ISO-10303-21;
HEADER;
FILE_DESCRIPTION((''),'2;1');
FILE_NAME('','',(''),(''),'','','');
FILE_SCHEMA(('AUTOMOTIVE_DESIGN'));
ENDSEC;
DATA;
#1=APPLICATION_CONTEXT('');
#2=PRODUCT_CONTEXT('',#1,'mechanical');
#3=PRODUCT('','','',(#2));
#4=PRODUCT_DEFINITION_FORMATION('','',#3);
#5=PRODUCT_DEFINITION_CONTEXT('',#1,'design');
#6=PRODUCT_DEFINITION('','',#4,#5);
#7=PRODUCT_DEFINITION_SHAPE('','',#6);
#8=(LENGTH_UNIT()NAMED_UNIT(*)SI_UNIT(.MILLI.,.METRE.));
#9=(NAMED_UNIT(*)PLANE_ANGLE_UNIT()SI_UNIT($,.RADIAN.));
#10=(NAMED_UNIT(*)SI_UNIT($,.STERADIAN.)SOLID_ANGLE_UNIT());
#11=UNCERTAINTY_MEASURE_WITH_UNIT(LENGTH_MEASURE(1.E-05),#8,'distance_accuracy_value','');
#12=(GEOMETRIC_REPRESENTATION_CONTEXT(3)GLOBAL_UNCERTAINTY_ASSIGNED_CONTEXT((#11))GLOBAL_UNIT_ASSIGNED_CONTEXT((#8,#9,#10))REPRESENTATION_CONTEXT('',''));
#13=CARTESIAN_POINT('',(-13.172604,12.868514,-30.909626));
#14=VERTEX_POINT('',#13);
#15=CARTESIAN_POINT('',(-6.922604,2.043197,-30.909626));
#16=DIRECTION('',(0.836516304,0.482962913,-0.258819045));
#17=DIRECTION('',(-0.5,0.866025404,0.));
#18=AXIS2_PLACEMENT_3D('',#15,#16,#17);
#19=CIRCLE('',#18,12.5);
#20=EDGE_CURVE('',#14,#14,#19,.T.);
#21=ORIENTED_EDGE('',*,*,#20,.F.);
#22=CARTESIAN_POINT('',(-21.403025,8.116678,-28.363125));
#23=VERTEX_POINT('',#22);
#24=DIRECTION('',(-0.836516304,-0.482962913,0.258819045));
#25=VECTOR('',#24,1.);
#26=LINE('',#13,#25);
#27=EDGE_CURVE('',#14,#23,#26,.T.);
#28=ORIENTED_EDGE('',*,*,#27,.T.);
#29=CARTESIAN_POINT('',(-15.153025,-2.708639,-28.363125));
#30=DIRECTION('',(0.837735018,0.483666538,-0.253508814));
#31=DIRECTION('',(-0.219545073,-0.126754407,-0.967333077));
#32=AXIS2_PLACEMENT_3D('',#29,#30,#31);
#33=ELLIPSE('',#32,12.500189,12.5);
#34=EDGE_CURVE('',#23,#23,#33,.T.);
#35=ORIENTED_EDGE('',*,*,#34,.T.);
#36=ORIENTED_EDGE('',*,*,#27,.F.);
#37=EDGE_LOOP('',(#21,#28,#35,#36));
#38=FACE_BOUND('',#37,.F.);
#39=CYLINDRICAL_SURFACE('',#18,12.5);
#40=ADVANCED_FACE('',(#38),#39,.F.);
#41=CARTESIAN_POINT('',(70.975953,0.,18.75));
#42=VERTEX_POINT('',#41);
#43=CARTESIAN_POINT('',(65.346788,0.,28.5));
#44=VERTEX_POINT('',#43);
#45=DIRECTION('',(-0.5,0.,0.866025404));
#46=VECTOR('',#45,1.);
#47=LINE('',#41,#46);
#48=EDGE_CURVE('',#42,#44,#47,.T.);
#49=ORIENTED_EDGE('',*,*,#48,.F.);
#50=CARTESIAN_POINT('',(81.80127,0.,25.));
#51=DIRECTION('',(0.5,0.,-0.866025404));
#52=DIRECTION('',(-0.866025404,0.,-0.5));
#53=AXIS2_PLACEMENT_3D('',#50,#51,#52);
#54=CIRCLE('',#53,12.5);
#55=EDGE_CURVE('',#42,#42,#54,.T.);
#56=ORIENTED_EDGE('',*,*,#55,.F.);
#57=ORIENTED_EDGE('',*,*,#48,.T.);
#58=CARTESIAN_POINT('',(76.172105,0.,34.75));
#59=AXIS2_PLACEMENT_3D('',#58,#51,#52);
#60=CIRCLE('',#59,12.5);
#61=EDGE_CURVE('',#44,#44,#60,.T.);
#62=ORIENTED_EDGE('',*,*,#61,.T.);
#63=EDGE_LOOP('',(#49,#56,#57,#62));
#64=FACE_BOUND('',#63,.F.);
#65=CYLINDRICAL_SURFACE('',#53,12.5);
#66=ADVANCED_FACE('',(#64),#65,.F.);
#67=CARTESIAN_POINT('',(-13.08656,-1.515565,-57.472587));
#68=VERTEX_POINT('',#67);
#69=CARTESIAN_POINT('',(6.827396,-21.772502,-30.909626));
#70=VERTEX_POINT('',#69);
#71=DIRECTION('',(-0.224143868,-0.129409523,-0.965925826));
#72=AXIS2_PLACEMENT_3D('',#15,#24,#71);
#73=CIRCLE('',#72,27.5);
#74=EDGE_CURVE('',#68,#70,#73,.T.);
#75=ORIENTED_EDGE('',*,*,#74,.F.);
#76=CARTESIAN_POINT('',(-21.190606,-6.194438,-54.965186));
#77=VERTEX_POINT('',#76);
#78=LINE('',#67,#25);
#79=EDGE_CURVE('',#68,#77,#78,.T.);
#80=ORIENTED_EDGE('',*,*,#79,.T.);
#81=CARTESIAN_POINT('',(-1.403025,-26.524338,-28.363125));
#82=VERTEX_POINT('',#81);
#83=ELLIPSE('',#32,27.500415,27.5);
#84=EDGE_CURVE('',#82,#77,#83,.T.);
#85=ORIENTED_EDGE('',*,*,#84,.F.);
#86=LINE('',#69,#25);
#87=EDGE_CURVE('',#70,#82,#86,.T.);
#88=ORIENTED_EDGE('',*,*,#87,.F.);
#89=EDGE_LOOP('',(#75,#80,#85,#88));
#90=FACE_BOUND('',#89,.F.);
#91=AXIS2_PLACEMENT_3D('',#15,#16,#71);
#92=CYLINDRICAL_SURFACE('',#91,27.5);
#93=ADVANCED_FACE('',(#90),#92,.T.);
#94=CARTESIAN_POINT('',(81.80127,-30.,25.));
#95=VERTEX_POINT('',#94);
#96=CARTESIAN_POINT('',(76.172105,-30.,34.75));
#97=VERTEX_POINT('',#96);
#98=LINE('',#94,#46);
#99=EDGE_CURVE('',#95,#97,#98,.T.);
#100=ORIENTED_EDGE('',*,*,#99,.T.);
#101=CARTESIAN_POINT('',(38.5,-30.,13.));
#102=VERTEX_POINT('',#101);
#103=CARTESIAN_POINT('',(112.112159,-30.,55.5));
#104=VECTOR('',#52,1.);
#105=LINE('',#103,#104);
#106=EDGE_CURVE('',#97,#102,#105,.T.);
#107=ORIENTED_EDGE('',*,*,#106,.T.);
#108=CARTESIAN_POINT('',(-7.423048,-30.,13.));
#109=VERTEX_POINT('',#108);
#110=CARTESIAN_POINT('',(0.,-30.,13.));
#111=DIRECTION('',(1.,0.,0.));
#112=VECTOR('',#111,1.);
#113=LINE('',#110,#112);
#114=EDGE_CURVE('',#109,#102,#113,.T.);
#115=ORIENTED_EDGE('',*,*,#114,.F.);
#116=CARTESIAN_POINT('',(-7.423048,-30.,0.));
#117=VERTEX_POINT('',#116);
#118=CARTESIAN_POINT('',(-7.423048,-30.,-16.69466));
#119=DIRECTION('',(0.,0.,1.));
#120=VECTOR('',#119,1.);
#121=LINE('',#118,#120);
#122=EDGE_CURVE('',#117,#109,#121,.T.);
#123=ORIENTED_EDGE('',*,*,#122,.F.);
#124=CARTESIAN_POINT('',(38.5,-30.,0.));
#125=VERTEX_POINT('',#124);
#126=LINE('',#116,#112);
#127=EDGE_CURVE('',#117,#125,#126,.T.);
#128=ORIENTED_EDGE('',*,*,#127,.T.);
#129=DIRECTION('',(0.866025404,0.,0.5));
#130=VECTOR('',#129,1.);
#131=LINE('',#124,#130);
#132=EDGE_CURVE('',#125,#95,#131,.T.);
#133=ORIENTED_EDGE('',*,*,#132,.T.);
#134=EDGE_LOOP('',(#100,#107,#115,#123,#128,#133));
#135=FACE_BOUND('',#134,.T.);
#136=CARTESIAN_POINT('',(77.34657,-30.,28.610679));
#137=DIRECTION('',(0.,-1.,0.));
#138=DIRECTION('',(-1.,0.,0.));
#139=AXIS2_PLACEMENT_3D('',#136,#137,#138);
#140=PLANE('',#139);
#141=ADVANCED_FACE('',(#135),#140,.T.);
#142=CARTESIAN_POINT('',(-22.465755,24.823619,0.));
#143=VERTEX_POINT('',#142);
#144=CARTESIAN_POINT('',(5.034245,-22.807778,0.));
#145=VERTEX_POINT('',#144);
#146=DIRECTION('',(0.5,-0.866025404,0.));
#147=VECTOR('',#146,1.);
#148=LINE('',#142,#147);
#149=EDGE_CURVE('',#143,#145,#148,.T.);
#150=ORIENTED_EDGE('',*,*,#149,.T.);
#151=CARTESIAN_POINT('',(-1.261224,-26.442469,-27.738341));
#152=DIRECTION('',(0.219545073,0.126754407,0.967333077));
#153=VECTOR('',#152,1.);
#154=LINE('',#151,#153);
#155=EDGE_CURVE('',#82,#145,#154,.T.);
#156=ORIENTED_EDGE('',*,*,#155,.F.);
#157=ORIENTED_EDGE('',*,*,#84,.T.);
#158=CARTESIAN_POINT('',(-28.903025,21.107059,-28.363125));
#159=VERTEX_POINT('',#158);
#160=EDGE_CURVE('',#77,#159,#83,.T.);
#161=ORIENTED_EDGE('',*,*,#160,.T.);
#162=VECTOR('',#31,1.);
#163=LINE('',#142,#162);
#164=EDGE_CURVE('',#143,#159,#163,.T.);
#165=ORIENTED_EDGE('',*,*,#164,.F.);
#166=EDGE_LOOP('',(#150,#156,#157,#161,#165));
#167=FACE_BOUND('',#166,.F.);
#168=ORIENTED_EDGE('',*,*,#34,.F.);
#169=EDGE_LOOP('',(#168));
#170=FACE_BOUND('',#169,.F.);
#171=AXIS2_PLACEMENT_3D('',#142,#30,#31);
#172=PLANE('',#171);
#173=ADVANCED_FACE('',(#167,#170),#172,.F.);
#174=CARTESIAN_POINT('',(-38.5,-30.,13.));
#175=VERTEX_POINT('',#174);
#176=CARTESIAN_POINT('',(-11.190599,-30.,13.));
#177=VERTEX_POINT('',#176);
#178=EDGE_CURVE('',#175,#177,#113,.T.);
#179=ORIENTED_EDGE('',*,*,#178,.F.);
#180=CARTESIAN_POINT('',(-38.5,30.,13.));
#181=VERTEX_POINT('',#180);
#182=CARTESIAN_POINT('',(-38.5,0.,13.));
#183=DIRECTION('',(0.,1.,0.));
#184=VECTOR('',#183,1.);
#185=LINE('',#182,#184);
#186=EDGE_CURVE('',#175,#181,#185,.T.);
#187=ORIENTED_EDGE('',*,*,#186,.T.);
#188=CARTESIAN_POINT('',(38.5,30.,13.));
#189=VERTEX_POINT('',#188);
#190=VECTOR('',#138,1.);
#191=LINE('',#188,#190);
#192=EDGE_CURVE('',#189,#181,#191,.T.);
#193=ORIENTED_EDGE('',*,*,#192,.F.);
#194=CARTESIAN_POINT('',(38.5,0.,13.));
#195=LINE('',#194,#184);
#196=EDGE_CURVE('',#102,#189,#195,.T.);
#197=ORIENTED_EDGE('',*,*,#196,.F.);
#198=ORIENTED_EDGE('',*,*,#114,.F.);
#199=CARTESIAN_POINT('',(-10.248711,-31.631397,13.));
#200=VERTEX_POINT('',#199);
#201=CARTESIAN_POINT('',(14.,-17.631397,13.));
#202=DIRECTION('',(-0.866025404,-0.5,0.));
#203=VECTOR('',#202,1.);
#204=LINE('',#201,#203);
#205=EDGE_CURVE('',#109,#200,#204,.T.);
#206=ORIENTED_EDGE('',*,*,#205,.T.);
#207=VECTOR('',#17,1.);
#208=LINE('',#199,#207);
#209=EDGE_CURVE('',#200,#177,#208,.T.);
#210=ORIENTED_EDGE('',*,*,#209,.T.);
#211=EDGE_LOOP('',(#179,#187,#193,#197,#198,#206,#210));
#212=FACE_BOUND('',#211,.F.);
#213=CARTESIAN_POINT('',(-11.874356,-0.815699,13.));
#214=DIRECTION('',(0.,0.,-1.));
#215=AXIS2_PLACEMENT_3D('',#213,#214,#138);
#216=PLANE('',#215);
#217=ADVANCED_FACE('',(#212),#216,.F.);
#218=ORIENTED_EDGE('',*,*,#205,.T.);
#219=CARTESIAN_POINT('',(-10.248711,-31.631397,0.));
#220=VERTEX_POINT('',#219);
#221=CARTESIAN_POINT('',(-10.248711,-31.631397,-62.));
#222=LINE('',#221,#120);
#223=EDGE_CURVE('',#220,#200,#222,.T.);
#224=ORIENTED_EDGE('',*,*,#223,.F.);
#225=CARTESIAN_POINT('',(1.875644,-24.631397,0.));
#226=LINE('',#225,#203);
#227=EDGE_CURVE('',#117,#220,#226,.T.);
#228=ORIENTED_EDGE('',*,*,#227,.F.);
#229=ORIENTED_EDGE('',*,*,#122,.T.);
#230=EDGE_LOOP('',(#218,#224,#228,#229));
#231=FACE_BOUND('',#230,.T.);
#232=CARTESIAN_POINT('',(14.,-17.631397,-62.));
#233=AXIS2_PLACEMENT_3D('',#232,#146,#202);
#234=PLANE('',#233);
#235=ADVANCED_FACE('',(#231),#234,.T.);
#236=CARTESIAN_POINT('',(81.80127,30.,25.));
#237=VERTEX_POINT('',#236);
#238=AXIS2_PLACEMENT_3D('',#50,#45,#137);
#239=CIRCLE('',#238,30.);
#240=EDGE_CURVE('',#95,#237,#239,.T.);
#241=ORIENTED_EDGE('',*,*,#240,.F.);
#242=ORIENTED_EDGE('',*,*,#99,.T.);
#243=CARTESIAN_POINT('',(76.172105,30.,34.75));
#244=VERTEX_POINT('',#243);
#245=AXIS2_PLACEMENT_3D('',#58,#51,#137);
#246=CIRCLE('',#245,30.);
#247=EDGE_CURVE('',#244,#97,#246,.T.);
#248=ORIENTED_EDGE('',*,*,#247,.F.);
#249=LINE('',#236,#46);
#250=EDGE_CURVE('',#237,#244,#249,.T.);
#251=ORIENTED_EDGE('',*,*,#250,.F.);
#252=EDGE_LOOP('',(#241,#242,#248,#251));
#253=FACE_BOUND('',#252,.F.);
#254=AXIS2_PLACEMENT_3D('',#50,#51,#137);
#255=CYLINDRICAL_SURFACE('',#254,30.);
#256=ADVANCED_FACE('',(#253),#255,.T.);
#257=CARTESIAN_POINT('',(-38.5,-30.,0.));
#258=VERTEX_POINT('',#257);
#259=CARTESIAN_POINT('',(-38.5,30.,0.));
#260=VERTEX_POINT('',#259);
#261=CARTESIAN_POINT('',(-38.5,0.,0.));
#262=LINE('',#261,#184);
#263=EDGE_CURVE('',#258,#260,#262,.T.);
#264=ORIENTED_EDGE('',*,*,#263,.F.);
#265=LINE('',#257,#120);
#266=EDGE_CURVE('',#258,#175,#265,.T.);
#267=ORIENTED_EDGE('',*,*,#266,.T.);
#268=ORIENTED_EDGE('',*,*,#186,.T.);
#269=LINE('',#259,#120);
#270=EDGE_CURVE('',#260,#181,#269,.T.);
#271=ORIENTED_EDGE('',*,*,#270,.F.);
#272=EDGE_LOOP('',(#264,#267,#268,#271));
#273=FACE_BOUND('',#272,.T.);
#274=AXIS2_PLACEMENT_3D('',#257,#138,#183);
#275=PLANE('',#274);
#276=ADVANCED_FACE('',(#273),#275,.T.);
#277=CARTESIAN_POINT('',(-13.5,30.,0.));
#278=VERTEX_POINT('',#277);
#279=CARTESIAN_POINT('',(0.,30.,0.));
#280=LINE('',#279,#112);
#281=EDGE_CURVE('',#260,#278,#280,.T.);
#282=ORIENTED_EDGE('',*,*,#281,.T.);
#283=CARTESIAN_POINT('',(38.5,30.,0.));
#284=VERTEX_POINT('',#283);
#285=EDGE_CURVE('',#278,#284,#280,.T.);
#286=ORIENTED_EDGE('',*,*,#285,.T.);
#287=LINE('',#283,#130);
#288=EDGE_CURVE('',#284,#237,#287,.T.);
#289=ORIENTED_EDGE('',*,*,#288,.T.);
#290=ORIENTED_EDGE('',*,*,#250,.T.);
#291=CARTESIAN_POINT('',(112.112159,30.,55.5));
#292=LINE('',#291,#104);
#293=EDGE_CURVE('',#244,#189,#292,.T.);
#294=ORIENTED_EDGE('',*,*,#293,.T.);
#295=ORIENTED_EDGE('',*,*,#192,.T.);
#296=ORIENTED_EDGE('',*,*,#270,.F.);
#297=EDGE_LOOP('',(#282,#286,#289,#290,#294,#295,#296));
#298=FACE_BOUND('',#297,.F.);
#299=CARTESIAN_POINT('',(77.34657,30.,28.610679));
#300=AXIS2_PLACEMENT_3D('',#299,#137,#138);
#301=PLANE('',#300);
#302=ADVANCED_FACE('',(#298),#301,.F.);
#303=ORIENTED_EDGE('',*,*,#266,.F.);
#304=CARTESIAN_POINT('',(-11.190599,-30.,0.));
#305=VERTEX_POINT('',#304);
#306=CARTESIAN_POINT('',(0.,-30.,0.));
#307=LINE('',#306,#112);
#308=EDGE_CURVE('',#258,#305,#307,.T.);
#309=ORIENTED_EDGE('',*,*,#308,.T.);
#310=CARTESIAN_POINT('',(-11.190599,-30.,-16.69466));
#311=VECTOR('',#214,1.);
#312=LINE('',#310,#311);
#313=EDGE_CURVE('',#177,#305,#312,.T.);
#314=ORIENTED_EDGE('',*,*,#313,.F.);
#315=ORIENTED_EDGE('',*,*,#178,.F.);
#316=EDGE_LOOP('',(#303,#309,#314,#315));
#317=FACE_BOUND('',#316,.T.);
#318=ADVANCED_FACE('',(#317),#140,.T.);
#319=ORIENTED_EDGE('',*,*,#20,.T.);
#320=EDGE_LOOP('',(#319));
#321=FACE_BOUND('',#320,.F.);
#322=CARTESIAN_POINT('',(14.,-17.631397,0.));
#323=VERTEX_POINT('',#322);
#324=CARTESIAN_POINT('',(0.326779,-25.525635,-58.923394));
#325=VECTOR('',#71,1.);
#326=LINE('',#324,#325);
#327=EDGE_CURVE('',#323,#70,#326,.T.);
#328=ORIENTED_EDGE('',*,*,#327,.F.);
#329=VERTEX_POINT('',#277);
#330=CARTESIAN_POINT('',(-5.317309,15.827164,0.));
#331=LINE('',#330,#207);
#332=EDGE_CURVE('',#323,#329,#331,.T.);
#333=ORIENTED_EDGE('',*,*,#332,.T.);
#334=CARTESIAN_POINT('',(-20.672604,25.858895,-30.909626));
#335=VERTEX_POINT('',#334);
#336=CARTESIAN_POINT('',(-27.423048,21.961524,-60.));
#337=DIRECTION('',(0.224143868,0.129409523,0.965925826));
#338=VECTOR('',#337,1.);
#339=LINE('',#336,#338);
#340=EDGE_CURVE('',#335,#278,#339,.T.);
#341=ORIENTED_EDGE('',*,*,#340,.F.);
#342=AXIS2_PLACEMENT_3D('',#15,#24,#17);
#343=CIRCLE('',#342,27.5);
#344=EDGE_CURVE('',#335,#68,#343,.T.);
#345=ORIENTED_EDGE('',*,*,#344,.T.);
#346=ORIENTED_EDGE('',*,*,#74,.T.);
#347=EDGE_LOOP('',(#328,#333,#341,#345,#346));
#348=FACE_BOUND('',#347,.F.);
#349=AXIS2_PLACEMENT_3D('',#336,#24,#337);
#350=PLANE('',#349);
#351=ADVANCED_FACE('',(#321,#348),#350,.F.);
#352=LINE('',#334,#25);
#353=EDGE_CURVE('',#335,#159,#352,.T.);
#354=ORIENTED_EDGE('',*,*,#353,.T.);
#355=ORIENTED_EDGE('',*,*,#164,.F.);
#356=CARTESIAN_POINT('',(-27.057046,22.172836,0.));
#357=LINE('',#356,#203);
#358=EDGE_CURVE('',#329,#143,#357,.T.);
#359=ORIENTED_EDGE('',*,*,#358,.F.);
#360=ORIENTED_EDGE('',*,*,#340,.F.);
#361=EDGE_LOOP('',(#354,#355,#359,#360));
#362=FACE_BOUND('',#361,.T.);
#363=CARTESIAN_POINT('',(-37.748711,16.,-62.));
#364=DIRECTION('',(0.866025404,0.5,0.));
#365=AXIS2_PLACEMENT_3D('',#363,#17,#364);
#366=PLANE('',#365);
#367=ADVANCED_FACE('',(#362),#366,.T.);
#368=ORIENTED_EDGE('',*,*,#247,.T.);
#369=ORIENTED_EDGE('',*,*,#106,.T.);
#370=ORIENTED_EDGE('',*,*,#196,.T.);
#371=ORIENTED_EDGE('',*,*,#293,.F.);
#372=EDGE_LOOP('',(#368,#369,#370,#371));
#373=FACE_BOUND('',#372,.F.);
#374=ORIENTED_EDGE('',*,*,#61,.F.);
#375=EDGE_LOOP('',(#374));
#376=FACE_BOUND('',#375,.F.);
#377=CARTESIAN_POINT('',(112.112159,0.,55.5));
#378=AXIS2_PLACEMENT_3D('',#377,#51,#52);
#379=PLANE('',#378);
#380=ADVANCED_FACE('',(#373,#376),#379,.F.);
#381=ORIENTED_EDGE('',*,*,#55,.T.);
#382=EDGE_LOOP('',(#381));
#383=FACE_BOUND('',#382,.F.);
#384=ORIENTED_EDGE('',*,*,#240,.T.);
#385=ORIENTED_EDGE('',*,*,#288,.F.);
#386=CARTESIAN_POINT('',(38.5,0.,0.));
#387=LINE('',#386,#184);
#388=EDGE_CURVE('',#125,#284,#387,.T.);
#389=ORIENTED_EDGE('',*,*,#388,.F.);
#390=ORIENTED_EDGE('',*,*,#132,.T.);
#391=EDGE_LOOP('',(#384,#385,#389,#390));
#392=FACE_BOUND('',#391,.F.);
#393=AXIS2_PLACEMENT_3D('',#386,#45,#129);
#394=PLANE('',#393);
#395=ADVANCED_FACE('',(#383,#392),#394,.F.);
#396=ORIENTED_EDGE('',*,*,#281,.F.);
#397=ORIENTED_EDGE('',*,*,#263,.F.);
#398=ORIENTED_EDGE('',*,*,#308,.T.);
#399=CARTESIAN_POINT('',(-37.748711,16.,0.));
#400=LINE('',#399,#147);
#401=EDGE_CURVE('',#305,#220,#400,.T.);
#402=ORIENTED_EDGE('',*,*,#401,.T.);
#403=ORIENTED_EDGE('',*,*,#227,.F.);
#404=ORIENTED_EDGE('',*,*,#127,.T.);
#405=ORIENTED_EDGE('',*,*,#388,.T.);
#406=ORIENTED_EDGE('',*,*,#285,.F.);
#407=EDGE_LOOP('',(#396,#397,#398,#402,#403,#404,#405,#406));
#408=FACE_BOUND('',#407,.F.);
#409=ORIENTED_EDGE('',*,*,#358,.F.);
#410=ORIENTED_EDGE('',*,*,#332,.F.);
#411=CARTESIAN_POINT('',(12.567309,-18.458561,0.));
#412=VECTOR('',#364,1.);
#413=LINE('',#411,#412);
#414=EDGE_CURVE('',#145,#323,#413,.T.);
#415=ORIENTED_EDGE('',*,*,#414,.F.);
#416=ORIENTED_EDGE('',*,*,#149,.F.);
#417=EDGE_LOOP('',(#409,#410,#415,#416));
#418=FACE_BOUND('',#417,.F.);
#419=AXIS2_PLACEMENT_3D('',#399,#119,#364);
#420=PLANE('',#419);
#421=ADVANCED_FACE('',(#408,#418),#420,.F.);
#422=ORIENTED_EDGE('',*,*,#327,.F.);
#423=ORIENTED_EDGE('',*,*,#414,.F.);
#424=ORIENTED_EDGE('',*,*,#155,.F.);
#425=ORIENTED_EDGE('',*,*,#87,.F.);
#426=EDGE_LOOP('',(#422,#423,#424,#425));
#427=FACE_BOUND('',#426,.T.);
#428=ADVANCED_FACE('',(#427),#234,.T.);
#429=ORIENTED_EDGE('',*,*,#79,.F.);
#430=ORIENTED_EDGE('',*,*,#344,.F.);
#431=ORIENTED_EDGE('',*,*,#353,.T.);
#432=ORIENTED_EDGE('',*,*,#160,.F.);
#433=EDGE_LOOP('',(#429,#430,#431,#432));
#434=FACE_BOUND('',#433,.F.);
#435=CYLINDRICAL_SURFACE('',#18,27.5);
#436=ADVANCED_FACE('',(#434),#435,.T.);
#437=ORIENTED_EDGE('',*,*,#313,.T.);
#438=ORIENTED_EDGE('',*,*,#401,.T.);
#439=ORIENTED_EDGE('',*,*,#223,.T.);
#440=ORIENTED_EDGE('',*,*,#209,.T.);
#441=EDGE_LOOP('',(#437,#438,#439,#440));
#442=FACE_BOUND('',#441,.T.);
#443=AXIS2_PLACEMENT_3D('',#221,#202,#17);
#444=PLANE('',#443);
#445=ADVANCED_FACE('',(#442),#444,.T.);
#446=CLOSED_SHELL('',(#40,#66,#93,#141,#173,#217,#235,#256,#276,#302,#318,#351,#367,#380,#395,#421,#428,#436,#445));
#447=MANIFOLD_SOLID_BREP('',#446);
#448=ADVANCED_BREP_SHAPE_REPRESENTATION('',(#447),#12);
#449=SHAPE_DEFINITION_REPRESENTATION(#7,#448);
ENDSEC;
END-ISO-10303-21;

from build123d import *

# Parameters (mm, degrees)
BASE_PLATE_SKETCH_W         = 77
BASE_PLATE_SKETCH_H         = 60
BASE_PLATE_60X77X13_DEPTH   = 13
UPPER_EYE_LUG_DEPTH         = 30
UPPER_LUG_CUT_SKETCH_R      = 12.5
UPPER_LUG_CUT_DEPTH         = 13
LOWER_EYE_LUG_DEPTH         = 13
LOWER_EYE_LUG_DEPTH_BACK    = 62
LOWER_LUG_PROFILE_CUT_DEPTH = 62
LOWER_LUG_TRIM_SKETCH_R     = 12.5
LOWER_LUG_TRIM_CUT_DEPTH    = 62


with BuildPart() as part:
    # Base Plate Sketch → Base Plate 60x77x13 (new body)
    with BuildSketch(Plane.XY):
        Rectangle(BASE_PLATE_SKETCH_W, BASE_PLATE_SKETCH_H)
    extrude(amount=BASE_PLATE_60X77X13_DEPTH)

    # Upper Lug Sketch → Upper Eye Lug (add, symmetric)
    with BuildSketch(Plane(origin=(0, 0, 0), x_dir=(1, 0, 0), z_dir=(0, 1, 0))):
        Polygon((38.5, -13), (38.5, 0), (120.77241336, -47.5), (112.112159322, -55.5), align=None)
    extrude(amount=UPPER_EYE_LUG_DEPTH, both=True)

    # Upper Lug Cut Sketch → Upper Lug Cut (cut)
    with BuildSketch(Plane(origin=(9.625, 0, -16.670989023), x_dir=(-0.8660254037844419, 0, -0.49999999999999434), z_dir=(0.49999999999999434, 0, -0.8660254037844419))):
        with BuildLine():
            Line((-128.341978046, 30), (-128.341978046, -30))
            Line((-128.341978046, -30), (-83.341978046, -30))
            ThreePointArc((-83.341978046, -30), (-113.341978046, 0), (-83.341978046, 30))
            Line((-83.341978046, 30), (-128.341978046, 30))
        make_face()
        with Locations((-83.341978046, 0)):
            Circle(UPPER_LUG_CUT_SKETCH_R)
    extrude(amount=-UPPER_LUG_CUT_DEPTH, mode=Mode.SUBTRACT)

    # Lower Lug Sketch → Lower Eye Lug (add, two sides: drawn at the far end of the back side and taken through both)
    with BuildSketch(Plane.XY.offset(-LOWER_EYE_LUG_DEPTH_BACK)):
        Polygon((14, -17.631397208), (-10.248711306, -31.631397208), (-37.748711306, 16), (-13.5, 30), align=None)
    extrude(amount=LOWER_EYE_LUG_DEPTH + LOWER_EYE_LUG_DEPTH_BACK)

    # Lower Lug Profile Cut Sketch → Lower Lug Profile Cut (cut)
    with BuildSketch(Plane(origin=(-16.365381057, 28.345671476, 0), x_dir=(0.8660254037844398, 0.4999999999999981, 0), z_dir=(-0.49999999999999817, 0.8660254037844398, 0))):
        Polygon((-7.044104755, 0), (-22.768294497, 60), (-12.768294497, 60), (3.308657049, 0), (3.308657049, 62), (-24.691342951, 62), (-24.691342951, 0), align=None)
    extrude(amount=-LOWER_LUG_PROFILE_CUT_DEPTH, mode=Mode.SUBTRACT)

    # Lower Lug Trim Sketch → Lower Lug Trim Cut (cut)
    with BuildSketch(Plane(origin=(2.673436922, 1.543509526, -0.827164262), x_dir=(-0.22414386804201733, -0.129409522551262, -0.9659258262890672), z_dir=(0.836516303737808, 0.48296291314453194, -0.258819045102525))):
        with BuildLine():
            Line((31.143656542, -22.269237886), (61.260227367, -22.269237886))
            Line((61.260227367, -22.269237886), (61.260227367, 32.730762114))
            Line((61.260227367, 32.730762114), (31.143656542, 32.730762114))
            ThreePointArc((31.143656542, 32.730762114), (50.589093025, 24.676198596), (58.643656542, 5.230762114))
            ThreePointArc((58.643656542, 5.230762114), (50.589093025, -14.214674369), (31.143656542, -22.269237886))
        make_face()
        with Locations(Location((31.143656542, 5.230762114, 0), (0, 0, 90))):
            Circle(LOWER_LUG_TRIM_SKETCH_R)
    extrude(amount=-LOWER_LUG_TRIM_CUT_DEPTH, mode=Mode.SUBTRACT)


with BuildPart() as body_2:
    # of the pieces the cut leaves, the one that is kept (lower_lug_trim_cut_keep)
    add(part.part.solids().sort_by_distance((-38.5, 30, 0))[0])


solid = body_2.part
